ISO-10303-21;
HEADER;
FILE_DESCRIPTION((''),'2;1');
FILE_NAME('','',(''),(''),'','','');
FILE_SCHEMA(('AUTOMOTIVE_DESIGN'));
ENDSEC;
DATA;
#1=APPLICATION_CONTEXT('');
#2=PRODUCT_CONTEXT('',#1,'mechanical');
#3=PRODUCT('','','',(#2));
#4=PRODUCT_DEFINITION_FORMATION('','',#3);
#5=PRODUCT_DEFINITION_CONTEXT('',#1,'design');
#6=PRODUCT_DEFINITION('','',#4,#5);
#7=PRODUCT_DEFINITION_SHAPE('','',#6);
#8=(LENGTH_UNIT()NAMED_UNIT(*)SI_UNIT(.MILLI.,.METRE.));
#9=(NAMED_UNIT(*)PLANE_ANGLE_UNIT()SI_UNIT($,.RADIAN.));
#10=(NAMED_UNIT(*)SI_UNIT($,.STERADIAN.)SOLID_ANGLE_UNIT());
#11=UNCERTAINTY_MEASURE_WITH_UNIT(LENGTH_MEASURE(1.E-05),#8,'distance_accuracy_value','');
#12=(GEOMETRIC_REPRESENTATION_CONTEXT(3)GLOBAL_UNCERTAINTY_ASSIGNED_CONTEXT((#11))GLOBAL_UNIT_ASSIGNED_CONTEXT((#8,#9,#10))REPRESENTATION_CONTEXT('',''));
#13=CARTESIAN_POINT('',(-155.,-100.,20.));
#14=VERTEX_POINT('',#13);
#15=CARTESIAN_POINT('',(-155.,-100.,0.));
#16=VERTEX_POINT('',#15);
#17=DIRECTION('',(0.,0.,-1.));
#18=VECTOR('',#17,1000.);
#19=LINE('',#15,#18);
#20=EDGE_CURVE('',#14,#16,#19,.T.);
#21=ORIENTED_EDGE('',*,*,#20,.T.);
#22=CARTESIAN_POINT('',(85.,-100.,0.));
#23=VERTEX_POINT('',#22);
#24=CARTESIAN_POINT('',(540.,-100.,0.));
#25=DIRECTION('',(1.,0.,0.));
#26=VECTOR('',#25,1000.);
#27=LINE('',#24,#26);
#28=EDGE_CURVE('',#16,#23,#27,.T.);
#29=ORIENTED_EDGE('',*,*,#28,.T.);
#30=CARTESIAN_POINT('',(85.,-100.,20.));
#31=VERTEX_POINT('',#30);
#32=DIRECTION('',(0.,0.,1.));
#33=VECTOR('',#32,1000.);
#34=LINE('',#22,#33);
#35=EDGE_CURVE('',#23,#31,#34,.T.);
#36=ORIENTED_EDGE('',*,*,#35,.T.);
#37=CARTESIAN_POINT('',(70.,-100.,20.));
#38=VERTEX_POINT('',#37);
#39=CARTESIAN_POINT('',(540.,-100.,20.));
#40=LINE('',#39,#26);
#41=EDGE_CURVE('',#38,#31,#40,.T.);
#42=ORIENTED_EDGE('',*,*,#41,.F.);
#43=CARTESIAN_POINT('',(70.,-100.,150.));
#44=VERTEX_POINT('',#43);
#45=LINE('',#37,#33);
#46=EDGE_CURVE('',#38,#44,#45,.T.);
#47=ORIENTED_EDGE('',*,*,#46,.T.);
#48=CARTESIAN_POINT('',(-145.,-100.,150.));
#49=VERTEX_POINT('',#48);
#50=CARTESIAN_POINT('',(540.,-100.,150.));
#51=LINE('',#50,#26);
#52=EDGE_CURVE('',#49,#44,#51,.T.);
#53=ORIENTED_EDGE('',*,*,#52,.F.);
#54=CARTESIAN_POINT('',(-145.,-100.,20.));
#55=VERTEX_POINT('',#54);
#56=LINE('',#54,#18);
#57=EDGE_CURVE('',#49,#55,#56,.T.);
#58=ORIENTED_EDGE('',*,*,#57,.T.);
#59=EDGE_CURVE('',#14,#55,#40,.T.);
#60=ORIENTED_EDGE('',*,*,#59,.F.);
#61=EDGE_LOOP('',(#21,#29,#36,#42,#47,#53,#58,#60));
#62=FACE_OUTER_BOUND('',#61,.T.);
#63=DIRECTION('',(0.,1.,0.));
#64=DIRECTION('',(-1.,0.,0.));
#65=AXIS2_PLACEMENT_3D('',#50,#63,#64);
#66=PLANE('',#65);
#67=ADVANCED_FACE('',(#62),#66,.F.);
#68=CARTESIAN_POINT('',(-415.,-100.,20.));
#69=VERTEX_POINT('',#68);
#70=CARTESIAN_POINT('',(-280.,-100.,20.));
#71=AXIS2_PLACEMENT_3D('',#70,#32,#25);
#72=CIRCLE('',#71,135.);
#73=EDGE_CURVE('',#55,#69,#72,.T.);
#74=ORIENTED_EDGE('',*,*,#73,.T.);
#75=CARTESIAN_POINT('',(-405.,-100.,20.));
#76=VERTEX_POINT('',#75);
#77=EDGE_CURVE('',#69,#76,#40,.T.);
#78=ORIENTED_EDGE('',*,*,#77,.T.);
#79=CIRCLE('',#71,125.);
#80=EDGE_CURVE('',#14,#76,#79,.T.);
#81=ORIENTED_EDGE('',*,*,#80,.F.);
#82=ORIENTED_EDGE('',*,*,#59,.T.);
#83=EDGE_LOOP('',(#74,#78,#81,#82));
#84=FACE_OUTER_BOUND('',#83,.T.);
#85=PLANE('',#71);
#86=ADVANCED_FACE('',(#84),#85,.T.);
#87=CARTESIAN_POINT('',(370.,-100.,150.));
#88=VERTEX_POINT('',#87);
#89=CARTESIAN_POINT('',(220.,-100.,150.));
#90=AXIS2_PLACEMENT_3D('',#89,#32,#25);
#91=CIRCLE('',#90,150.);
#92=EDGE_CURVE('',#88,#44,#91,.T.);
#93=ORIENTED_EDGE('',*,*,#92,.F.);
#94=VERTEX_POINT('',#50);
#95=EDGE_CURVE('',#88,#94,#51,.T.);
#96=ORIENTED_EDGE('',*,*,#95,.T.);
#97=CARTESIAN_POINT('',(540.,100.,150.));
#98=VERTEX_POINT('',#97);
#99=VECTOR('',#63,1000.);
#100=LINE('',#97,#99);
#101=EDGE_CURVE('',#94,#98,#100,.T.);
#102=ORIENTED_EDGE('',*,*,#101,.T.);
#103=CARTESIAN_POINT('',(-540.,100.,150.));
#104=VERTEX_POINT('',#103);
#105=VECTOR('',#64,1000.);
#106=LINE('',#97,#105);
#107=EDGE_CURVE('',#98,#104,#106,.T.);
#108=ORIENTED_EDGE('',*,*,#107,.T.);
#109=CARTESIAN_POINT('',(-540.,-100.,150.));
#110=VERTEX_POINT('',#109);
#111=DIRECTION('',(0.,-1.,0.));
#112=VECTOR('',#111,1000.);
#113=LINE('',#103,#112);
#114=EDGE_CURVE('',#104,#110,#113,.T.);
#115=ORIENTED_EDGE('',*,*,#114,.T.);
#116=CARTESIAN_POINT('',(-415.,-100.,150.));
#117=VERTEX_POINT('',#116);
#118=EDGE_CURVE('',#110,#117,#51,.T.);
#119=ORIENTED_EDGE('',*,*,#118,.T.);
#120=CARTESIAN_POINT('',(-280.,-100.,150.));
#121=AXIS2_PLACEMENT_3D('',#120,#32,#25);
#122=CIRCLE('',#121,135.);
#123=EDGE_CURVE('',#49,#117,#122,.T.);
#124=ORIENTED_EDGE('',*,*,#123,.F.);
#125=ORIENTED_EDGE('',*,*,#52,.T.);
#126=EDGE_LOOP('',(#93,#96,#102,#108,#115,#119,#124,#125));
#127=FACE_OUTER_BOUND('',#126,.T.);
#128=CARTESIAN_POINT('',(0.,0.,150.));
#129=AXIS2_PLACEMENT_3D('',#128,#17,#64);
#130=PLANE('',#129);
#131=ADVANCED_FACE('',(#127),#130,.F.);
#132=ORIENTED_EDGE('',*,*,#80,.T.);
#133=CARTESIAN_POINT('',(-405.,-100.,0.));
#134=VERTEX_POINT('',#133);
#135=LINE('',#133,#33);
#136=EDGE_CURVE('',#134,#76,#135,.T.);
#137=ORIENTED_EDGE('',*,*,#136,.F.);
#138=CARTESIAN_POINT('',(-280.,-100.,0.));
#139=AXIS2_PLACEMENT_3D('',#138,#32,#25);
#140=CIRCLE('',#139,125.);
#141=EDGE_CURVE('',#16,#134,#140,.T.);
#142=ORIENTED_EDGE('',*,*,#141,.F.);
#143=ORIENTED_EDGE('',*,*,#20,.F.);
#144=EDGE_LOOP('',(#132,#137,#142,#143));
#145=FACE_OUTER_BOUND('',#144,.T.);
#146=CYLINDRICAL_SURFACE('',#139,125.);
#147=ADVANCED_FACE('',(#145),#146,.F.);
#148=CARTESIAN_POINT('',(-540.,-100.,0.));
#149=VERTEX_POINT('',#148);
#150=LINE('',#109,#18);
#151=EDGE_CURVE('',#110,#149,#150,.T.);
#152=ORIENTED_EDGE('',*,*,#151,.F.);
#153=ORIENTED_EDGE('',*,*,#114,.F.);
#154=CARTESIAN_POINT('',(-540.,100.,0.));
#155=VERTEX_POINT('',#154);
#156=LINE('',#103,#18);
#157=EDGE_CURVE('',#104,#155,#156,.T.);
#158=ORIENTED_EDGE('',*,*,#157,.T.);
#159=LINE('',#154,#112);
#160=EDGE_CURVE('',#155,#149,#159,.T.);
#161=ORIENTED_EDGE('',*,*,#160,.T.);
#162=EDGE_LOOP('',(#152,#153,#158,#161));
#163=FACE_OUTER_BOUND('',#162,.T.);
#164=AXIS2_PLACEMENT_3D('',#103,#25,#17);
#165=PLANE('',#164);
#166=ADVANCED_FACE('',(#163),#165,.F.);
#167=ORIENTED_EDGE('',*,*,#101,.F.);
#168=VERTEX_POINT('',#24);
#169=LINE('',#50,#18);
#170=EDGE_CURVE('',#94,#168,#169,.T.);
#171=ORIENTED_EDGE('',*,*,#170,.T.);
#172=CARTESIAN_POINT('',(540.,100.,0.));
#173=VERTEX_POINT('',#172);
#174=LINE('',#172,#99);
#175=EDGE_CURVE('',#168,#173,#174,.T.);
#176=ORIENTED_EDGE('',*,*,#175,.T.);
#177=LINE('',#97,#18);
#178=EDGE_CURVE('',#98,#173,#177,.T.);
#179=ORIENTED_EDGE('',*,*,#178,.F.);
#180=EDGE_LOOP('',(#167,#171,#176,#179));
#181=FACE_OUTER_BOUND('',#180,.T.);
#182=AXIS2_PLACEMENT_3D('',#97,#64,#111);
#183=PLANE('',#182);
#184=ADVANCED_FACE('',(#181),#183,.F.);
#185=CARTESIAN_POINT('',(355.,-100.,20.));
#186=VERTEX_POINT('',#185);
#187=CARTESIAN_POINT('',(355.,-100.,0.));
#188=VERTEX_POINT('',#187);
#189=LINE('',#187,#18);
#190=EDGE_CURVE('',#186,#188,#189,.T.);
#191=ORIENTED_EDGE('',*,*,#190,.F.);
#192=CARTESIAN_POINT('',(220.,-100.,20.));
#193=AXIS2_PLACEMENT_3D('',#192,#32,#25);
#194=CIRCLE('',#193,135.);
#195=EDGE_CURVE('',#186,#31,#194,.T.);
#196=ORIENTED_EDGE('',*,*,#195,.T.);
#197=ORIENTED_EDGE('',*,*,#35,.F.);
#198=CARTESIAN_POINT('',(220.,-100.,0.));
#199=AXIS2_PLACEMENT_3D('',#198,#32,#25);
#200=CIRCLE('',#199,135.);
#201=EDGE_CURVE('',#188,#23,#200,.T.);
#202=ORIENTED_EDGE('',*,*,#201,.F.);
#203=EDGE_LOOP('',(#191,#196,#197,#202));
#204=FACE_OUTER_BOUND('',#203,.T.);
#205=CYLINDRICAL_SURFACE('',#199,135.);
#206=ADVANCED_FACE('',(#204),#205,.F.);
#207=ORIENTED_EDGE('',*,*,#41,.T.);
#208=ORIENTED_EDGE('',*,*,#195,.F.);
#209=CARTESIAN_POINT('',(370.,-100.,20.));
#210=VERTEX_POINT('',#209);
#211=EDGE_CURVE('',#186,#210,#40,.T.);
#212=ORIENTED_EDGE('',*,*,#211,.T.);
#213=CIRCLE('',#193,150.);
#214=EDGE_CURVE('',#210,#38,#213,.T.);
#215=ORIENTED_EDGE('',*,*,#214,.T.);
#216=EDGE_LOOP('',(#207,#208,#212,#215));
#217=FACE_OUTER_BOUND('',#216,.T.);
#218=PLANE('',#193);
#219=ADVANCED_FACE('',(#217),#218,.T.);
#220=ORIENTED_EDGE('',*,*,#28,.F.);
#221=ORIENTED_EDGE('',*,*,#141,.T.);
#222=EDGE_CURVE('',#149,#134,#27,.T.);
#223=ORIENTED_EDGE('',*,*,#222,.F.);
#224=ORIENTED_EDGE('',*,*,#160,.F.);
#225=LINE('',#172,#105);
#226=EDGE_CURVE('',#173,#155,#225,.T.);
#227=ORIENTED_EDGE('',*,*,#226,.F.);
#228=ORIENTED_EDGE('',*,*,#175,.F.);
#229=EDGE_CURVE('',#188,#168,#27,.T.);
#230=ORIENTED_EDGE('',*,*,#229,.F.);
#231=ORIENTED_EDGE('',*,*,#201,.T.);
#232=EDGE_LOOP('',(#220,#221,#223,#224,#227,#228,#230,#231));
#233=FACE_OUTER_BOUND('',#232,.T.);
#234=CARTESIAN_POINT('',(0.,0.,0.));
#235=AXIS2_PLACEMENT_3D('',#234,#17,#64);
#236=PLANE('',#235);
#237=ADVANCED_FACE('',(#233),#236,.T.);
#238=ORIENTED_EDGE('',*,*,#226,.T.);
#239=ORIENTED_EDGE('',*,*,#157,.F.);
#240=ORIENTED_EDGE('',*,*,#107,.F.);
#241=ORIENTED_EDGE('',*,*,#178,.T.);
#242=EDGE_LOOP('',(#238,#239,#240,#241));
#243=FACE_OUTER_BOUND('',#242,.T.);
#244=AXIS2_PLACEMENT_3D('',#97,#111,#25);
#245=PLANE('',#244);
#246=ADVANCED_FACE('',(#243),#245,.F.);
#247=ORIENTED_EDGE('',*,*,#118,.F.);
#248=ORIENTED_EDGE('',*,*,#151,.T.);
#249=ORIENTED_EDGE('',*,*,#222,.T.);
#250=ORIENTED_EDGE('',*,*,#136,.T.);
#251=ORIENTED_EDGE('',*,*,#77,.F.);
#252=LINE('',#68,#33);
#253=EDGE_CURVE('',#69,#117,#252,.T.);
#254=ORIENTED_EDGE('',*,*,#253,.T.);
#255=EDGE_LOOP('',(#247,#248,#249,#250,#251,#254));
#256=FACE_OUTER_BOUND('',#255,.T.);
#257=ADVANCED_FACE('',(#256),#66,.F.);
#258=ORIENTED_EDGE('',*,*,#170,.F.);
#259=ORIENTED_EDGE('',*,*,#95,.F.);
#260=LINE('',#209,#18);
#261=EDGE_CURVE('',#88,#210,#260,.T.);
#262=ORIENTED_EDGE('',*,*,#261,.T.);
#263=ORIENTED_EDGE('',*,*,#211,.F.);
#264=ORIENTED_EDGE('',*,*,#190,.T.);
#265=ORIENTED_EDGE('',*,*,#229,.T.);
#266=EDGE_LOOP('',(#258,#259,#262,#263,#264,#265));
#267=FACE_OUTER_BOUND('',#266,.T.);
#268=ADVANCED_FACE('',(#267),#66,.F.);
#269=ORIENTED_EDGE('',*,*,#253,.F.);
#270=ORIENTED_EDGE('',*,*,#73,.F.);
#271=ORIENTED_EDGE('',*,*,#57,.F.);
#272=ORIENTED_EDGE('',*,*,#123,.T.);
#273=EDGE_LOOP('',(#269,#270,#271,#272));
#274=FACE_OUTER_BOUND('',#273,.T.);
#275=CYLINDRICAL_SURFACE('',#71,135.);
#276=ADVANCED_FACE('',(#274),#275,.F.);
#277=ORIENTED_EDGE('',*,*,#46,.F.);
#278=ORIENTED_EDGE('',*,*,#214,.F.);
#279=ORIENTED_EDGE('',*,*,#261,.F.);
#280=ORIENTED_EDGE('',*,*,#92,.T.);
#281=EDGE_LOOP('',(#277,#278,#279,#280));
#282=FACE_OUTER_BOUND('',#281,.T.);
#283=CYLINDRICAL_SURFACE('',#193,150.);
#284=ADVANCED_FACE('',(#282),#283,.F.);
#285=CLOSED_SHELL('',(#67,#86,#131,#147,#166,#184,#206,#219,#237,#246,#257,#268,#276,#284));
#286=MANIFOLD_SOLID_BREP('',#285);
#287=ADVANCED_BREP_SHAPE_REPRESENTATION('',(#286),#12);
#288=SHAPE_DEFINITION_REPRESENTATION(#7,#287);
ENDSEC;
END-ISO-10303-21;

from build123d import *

# Parameters (mm, degrees)
SKETCH_1_W               = 1080
SKETCH_1_H               = 200
EXTRUDE_1_DEPTH          = 150
SKETCH_2_R               = 135
SKETCH_2_R_2             = 150
CUT_EXTRUDE_1_DEPTH      = 130
CUT_EXTRUDE_2_DEPTH      = 570.2978131
CUT_EXTRUDE_2_DEPTH_BACK = 570.2978131
SKETCH_2_3_R             = 125
SKETCH_2_3_R_2           = 135


with BuildPart() as part:
    # 草图1 → 凸台-拉伸1 (new body)
    with BuildSketch(Plane.XY):
        Rectangle(SKETCH_1_W, SKETCH_1_H)
    extrude(amount=EXTRUDE_1_DEPTH)

    # 草图2 → 切除-拉伸1 (cut)
    with BuildSketch(Plane.XY.offset(150)):
        with Locations((-280, -100)):
            Circle(SKETCH_2_R)
        with Locations((220, -100)):
            Circle(SKETCH_2_R_2)
    extrude(amount=-CUT_EXTRUDE_1_DEPTH, mode=Mode.SUBTRACT)

    # 草图2<3> → 切除-拉伸2 (cut, two sides: drawn at the far end of the back side and taken through both)
    with BuildSketch(Plane.XY.offset(150).offset(-CUT_EXTRUDE_2_DEPTH_BACK)):
        with Locations((-280, -100)):
            Circle(SKETCH_2_3_R)
        with Locations((220, -100)):
            Circle(SKETCH_2_3_R_2)
    extrude(amount=CUT_EXTRUDE_2_DEPTH + CUT_EXTRUDE_2_DEPTH_BACK, mode=Mode.SUBTRACT)


solid = part.part
